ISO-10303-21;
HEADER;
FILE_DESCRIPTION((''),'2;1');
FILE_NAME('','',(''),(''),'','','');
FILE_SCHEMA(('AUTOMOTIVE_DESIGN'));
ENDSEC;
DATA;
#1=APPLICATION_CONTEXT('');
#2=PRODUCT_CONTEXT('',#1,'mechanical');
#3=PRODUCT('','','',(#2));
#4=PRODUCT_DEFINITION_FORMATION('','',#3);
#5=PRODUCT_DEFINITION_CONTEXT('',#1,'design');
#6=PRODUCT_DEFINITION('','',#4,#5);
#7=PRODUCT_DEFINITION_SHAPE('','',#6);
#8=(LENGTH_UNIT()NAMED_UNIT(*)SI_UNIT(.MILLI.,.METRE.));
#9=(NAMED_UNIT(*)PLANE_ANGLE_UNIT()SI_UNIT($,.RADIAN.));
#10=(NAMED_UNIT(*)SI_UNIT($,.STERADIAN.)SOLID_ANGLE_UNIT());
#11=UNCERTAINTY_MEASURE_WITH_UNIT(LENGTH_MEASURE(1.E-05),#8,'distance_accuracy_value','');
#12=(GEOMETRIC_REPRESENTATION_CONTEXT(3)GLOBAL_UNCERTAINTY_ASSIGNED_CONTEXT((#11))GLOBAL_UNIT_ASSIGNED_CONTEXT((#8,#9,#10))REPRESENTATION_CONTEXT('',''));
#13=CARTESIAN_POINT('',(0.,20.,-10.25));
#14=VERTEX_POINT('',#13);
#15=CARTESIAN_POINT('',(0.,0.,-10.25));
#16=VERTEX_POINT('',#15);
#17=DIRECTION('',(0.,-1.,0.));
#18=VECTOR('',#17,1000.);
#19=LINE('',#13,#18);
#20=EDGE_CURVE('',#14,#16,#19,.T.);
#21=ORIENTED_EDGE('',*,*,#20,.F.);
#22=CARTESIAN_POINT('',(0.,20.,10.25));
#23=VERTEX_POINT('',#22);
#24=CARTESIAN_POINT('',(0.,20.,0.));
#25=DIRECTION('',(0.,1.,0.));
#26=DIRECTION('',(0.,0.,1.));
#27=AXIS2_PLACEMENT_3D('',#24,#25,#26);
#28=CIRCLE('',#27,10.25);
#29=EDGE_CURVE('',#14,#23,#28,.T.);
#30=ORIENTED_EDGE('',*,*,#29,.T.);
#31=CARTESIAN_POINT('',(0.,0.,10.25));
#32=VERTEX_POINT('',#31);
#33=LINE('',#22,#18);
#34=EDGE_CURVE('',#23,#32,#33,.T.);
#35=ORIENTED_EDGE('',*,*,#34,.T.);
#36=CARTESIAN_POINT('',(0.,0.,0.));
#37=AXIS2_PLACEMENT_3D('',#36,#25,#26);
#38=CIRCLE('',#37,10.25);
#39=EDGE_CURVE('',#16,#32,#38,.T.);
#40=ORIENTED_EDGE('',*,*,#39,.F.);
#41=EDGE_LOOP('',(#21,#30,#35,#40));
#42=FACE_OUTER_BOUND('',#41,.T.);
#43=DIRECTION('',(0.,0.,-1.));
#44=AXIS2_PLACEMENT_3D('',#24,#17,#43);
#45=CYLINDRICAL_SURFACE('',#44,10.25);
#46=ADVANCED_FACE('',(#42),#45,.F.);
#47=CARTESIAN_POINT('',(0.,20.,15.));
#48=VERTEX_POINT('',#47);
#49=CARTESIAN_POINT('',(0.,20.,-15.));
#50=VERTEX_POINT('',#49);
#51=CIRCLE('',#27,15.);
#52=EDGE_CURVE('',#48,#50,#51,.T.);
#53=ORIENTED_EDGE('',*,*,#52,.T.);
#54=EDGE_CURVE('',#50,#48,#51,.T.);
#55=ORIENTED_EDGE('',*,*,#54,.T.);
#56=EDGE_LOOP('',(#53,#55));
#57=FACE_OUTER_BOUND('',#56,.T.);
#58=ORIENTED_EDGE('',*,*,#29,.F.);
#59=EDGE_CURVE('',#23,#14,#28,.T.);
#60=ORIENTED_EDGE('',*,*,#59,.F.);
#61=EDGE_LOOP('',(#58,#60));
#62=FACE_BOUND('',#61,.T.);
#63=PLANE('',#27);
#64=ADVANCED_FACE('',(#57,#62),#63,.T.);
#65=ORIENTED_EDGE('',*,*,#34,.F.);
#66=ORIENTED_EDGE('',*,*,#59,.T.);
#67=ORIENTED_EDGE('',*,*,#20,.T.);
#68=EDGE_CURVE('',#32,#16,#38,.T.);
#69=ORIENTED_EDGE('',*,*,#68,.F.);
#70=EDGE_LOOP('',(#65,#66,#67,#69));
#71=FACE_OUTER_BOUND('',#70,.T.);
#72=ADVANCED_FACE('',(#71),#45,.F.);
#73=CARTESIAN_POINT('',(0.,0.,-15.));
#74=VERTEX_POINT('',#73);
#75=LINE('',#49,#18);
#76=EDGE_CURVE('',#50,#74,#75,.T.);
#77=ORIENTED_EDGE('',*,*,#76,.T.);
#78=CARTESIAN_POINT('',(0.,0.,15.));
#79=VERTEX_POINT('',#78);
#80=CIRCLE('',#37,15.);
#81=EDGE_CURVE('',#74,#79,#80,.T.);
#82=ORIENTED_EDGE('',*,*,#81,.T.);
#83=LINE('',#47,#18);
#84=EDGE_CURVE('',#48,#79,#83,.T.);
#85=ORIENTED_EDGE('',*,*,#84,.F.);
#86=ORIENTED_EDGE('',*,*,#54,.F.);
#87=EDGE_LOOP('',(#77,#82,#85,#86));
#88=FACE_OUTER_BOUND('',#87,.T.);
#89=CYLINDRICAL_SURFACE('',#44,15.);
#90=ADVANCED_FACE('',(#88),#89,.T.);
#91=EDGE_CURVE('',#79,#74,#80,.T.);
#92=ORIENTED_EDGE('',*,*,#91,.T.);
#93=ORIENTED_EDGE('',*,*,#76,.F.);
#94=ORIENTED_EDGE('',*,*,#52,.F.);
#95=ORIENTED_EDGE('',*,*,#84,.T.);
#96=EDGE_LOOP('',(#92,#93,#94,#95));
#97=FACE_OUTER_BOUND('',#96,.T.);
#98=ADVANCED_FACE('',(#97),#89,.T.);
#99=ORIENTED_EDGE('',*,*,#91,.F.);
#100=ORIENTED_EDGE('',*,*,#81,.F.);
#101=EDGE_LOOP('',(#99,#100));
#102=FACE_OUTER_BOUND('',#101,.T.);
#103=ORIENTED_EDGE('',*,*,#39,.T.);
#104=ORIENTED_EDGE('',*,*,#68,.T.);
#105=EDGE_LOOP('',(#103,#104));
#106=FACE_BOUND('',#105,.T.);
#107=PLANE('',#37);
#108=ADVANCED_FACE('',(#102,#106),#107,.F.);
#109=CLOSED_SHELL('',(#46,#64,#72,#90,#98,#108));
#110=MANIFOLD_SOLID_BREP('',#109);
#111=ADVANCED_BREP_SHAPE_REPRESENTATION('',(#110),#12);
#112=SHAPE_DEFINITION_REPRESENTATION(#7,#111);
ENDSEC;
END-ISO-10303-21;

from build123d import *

# Parameters (mm, degrees)
SKETCH_1_R      = 15
SKETCH_1_R_2    = 10.25
EXTRUDE_1_DEPTH = 20


with BuildPart() as part:
    # 草图1 → 凸台-拉伸1 (new body)
    with BuildSketch(Plane(origin=(0, 0, 0), x_dir=(1, 0, 0), z_dir=(0, 1, 0))):
        with Locations(Location((0, 0, 0), (0, 0, 270))):
            Circle(SKETCH_1_R)
        with Locations(Location((0, 0, 0), (0, 0, 270))):
            Circle(SKETCH_1_R_2, mode=Mode.SUBTRACT)
    extrude(amount=EXTRUDE_1_DEPTH)


solid = part.part
